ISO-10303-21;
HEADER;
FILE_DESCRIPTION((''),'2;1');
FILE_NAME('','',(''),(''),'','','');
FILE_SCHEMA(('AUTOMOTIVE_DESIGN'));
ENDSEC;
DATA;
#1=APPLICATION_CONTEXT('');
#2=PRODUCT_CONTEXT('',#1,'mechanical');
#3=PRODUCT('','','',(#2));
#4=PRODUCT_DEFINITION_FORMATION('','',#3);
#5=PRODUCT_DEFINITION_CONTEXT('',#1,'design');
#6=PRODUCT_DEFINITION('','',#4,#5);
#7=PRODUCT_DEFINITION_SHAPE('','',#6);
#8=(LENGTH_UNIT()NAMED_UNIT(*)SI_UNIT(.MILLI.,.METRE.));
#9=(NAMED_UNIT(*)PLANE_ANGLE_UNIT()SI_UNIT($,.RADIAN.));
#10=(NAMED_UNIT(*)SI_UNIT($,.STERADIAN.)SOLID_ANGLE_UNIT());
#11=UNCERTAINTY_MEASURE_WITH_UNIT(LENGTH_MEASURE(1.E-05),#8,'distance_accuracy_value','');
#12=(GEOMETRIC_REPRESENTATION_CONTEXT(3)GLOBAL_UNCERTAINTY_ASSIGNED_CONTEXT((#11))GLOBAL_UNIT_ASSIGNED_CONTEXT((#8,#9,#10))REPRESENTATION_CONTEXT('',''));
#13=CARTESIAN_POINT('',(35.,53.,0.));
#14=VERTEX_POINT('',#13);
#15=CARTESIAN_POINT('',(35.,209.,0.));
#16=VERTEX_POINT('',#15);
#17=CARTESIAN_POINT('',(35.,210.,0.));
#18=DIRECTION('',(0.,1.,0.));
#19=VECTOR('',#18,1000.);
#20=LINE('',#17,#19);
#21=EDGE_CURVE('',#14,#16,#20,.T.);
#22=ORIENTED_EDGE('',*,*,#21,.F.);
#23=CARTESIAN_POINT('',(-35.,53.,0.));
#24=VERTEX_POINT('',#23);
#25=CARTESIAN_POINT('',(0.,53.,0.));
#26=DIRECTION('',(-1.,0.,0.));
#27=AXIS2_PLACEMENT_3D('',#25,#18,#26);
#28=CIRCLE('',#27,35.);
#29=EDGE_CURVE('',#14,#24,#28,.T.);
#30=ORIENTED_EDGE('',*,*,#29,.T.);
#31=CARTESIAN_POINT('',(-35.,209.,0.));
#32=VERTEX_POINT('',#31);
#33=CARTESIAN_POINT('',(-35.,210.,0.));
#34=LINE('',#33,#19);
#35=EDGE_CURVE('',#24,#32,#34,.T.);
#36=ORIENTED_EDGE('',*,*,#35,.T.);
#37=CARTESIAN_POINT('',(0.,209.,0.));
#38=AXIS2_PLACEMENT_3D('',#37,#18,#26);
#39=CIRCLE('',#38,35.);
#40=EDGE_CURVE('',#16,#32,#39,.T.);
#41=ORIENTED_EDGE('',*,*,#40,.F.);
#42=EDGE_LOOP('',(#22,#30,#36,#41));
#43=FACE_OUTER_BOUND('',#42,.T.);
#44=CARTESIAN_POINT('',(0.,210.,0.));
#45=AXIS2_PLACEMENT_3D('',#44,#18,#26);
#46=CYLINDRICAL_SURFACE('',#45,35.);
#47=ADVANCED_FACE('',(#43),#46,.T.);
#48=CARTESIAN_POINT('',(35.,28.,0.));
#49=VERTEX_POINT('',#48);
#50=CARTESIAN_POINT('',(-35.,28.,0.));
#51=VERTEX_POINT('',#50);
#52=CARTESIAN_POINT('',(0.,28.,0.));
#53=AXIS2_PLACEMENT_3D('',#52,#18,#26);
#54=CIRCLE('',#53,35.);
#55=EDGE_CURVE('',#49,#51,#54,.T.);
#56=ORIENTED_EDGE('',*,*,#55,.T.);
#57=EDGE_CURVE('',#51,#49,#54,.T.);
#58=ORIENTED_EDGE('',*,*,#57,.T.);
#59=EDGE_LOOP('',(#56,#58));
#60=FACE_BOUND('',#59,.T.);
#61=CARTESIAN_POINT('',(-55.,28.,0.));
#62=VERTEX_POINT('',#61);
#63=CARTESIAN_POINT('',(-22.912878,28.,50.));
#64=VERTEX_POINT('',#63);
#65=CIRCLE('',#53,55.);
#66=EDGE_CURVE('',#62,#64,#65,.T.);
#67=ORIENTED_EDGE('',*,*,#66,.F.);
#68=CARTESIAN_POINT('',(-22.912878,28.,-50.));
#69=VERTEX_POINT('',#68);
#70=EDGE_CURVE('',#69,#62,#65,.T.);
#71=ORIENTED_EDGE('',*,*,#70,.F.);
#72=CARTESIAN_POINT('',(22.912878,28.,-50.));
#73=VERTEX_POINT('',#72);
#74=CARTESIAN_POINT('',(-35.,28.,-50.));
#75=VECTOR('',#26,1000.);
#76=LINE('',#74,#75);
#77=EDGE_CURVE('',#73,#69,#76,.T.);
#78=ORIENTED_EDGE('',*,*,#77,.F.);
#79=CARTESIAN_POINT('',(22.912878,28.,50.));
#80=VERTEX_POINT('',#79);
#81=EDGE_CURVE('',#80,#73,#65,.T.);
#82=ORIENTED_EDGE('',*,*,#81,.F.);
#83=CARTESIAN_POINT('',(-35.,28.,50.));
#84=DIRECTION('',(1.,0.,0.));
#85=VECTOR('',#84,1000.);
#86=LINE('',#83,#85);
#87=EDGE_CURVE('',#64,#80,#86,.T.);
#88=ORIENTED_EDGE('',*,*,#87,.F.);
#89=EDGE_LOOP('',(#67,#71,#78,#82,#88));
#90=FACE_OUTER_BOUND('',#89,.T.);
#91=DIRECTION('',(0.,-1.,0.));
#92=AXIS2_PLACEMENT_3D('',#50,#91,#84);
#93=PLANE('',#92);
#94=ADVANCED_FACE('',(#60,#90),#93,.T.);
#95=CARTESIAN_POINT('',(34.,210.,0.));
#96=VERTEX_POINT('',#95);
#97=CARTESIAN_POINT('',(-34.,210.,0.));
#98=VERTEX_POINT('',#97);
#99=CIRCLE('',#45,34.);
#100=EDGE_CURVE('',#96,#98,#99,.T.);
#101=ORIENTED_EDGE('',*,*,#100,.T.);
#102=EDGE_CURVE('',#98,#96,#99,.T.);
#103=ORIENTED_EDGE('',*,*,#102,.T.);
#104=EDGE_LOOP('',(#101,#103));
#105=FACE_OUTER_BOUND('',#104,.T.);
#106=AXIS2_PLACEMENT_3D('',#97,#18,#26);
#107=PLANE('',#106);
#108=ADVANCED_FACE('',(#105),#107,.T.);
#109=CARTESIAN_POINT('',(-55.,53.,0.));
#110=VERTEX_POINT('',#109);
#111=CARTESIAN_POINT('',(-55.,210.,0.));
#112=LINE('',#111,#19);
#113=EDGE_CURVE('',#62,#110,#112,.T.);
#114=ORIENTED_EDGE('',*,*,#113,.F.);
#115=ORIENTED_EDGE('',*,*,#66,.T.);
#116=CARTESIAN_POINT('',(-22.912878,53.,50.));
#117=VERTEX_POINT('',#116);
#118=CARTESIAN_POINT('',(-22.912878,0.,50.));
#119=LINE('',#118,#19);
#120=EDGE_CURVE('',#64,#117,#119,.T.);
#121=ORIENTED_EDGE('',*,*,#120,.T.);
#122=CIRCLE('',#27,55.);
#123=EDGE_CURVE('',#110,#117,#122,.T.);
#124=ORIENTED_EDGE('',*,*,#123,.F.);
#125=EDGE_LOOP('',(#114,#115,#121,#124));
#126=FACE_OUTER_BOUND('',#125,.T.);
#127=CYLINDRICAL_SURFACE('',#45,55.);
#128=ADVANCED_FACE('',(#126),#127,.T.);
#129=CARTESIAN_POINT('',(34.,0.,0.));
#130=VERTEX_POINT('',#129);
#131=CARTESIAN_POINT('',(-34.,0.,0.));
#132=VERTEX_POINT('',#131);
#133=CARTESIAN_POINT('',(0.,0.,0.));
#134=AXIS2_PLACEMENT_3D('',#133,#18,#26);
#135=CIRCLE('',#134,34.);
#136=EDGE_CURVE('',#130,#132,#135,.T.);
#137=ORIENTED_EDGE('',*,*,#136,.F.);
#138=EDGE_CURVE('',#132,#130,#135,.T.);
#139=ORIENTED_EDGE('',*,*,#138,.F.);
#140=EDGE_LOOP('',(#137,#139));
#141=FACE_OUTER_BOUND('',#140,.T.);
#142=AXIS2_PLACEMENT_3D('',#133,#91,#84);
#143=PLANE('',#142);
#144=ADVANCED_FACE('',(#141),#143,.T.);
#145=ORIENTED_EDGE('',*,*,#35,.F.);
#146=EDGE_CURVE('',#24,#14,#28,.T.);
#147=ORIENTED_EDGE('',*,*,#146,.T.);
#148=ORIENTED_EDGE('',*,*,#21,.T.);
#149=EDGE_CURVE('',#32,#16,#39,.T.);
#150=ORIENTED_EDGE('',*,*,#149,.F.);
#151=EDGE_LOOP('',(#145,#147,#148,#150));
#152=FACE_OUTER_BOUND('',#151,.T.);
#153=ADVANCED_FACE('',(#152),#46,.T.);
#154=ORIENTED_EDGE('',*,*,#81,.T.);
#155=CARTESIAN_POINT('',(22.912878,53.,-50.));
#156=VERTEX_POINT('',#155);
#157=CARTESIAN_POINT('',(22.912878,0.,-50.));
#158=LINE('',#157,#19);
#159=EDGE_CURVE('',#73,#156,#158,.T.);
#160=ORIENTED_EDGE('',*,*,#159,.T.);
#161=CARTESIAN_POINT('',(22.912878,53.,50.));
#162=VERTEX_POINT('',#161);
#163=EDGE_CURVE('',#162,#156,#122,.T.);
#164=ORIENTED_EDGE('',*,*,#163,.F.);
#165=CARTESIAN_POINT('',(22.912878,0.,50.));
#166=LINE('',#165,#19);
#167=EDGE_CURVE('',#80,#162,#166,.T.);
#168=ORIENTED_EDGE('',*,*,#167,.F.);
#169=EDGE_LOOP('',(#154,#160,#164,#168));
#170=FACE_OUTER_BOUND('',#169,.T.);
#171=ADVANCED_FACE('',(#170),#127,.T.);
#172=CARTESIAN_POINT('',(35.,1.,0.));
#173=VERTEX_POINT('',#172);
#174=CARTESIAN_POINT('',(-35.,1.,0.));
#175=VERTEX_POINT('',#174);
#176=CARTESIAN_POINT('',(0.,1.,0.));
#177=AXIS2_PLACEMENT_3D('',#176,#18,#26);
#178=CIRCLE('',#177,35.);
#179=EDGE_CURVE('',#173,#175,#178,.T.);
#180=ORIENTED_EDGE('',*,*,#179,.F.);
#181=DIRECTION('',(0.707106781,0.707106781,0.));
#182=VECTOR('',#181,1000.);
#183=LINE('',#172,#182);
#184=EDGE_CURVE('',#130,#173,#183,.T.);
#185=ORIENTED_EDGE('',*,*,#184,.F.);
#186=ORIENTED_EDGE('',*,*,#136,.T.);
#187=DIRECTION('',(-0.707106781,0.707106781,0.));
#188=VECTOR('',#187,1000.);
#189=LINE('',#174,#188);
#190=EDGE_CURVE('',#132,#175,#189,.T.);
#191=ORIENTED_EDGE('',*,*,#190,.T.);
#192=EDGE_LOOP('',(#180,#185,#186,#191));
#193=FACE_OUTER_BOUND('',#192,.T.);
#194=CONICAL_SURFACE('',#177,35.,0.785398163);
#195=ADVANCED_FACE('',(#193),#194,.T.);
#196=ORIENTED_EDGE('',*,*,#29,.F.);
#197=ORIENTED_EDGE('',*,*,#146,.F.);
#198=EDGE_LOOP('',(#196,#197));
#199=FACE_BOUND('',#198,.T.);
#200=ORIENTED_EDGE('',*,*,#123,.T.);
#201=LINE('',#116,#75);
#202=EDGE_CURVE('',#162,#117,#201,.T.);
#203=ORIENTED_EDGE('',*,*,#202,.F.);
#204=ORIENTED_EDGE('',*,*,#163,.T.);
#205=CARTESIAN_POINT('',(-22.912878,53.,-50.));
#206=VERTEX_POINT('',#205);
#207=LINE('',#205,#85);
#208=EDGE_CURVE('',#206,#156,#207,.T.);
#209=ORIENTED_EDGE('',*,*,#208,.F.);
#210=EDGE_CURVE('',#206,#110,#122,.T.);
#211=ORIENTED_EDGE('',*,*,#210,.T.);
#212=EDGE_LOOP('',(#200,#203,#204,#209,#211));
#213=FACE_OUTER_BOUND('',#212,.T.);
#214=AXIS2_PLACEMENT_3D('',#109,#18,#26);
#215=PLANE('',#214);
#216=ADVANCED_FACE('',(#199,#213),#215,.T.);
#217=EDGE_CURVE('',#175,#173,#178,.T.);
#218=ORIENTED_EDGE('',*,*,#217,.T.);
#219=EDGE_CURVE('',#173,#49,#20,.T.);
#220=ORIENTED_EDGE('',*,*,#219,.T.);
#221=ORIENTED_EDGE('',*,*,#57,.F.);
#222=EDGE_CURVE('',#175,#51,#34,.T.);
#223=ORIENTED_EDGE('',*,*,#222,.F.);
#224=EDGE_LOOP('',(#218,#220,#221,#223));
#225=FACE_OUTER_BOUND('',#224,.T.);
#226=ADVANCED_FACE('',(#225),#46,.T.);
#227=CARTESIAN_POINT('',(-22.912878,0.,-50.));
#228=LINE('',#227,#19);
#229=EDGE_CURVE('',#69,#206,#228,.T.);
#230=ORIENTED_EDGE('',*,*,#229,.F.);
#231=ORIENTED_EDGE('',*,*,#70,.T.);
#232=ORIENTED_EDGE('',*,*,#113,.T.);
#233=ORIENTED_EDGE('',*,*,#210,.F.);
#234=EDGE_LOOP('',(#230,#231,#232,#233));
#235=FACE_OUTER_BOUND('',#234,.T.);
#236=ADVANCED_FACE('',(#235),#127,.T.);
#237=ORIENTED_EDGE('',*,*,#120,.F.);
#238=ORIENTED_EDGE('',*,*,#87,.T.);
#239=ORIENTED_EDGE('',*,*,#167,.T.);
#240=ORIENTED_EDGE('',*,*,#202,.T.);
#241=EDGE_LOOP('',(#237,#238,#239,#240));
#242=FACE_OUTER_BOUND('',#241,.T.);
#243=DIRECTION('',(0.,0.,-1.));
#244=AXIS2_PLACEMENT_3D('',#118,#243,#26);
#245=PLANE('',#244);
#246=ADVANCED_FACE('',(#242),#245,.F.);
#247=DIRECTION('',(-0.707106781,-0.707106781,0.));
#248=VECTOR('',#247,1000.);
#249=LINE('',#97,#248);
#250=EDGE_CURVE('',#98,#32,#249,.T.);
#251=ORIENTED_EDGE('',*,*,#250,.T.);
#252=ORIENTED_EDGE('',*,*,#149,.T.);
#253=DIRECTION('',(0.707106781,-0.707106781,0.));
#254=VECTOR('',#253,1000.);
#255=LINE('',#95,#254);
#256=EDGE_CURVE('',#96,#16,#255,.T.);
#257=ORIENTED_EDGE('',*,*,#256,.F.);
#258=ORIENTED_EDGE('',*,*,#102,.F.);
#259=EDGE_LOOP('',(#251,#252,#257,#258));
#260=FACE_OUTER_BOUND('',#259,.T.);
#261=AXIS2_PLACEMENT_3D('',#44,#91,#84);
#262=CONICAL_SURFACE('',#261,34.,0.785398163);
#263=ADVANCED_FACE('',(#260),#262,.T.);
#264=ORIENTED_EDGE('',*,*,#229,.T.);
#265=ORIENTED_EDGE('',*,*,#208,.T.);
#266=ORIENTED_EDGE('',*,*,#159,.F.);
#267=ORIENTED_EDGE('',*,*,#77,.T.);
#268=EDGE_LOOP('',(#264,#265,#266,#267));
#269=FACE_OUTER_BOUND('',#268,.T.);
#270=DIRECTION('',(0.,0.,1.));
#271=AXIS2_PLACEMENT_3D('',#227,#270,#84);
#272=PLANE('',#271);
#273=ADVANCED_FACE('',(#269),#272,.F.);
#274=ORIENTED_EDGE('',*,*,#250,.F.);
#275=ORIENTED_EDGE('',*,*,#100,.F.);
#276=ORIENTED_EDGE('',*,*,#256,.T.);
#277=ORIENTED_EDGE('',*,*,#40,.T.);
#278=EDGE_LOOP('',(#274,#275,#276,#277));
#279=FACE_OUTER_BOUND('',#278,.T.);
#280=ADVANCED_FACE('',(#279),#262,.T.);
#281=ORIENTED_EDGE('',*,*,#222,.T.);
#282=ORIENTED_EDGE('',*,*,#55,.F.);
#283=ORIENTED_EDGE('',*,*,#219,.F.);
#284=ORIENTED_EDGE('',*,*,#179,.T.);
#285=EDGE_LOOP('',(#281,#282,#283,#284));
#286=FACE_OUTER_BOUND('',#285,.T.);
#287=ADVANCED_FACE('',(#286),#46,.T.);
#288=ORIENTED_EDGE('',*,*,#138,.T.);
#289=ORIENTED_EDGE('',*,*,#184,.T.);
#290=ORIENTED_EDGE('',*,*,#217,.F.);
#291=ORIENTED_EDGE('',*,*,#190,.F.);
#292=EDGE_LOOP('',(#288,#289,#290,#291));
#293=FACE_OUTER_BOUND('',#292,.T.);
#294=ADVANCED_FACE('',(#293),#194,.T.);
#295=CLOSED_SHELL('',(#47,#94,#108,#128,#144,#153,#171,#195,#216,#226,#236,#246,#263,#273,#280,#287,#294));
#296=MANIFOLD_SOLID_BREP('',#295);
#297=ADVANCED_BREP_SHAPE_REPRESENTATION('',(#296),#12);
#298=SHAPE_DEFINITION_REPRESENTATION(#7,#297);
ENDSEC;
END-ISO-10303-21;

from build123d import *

# Parameters (mm, degrees)
CUT_EXTRUDE1_DEPTH = 176.211301005


with BuildPart() as part:
    # Sketch1 → Revolve1 (revolve)
    with BuildSketch(Plane.XY):
        Polygon((0, 0), (-34, 0), (-35, 1), (-35, 28), (-55, 28), (-55, 53), (-35, 53), (-35, 209), (-34, 210), (0, 210), align=None)
    revolve(axis=Axis((0, 210, 0), (0, -1, 0)))

    # Sketch2 → Cut-Extrude1 (cut, through all)
    with BuildSketch(Plane(origin=(0, 53, 0), x_dir=(1, 0, 0), z_dir=(0, 1, 0))):
        with BuildLine():
            Line((-22.912878475, 50), (22.912878475, 50))
            ThreePointArc((22.912878475, 50), (0, 55), (-22.912878475, 50))
        make_face()
        with BuildLine():
            Line((-22.912878475, -50), (22.912878475, -50))
            ThreePointArc((22.912878475, -50), (0, -55), (-22.912878475, -50))
        make_face()
    extrude(amount=-CUT_EXTRUDE1_DEPTH, mode=Mode.SUBTRACT)


solid = part.part
